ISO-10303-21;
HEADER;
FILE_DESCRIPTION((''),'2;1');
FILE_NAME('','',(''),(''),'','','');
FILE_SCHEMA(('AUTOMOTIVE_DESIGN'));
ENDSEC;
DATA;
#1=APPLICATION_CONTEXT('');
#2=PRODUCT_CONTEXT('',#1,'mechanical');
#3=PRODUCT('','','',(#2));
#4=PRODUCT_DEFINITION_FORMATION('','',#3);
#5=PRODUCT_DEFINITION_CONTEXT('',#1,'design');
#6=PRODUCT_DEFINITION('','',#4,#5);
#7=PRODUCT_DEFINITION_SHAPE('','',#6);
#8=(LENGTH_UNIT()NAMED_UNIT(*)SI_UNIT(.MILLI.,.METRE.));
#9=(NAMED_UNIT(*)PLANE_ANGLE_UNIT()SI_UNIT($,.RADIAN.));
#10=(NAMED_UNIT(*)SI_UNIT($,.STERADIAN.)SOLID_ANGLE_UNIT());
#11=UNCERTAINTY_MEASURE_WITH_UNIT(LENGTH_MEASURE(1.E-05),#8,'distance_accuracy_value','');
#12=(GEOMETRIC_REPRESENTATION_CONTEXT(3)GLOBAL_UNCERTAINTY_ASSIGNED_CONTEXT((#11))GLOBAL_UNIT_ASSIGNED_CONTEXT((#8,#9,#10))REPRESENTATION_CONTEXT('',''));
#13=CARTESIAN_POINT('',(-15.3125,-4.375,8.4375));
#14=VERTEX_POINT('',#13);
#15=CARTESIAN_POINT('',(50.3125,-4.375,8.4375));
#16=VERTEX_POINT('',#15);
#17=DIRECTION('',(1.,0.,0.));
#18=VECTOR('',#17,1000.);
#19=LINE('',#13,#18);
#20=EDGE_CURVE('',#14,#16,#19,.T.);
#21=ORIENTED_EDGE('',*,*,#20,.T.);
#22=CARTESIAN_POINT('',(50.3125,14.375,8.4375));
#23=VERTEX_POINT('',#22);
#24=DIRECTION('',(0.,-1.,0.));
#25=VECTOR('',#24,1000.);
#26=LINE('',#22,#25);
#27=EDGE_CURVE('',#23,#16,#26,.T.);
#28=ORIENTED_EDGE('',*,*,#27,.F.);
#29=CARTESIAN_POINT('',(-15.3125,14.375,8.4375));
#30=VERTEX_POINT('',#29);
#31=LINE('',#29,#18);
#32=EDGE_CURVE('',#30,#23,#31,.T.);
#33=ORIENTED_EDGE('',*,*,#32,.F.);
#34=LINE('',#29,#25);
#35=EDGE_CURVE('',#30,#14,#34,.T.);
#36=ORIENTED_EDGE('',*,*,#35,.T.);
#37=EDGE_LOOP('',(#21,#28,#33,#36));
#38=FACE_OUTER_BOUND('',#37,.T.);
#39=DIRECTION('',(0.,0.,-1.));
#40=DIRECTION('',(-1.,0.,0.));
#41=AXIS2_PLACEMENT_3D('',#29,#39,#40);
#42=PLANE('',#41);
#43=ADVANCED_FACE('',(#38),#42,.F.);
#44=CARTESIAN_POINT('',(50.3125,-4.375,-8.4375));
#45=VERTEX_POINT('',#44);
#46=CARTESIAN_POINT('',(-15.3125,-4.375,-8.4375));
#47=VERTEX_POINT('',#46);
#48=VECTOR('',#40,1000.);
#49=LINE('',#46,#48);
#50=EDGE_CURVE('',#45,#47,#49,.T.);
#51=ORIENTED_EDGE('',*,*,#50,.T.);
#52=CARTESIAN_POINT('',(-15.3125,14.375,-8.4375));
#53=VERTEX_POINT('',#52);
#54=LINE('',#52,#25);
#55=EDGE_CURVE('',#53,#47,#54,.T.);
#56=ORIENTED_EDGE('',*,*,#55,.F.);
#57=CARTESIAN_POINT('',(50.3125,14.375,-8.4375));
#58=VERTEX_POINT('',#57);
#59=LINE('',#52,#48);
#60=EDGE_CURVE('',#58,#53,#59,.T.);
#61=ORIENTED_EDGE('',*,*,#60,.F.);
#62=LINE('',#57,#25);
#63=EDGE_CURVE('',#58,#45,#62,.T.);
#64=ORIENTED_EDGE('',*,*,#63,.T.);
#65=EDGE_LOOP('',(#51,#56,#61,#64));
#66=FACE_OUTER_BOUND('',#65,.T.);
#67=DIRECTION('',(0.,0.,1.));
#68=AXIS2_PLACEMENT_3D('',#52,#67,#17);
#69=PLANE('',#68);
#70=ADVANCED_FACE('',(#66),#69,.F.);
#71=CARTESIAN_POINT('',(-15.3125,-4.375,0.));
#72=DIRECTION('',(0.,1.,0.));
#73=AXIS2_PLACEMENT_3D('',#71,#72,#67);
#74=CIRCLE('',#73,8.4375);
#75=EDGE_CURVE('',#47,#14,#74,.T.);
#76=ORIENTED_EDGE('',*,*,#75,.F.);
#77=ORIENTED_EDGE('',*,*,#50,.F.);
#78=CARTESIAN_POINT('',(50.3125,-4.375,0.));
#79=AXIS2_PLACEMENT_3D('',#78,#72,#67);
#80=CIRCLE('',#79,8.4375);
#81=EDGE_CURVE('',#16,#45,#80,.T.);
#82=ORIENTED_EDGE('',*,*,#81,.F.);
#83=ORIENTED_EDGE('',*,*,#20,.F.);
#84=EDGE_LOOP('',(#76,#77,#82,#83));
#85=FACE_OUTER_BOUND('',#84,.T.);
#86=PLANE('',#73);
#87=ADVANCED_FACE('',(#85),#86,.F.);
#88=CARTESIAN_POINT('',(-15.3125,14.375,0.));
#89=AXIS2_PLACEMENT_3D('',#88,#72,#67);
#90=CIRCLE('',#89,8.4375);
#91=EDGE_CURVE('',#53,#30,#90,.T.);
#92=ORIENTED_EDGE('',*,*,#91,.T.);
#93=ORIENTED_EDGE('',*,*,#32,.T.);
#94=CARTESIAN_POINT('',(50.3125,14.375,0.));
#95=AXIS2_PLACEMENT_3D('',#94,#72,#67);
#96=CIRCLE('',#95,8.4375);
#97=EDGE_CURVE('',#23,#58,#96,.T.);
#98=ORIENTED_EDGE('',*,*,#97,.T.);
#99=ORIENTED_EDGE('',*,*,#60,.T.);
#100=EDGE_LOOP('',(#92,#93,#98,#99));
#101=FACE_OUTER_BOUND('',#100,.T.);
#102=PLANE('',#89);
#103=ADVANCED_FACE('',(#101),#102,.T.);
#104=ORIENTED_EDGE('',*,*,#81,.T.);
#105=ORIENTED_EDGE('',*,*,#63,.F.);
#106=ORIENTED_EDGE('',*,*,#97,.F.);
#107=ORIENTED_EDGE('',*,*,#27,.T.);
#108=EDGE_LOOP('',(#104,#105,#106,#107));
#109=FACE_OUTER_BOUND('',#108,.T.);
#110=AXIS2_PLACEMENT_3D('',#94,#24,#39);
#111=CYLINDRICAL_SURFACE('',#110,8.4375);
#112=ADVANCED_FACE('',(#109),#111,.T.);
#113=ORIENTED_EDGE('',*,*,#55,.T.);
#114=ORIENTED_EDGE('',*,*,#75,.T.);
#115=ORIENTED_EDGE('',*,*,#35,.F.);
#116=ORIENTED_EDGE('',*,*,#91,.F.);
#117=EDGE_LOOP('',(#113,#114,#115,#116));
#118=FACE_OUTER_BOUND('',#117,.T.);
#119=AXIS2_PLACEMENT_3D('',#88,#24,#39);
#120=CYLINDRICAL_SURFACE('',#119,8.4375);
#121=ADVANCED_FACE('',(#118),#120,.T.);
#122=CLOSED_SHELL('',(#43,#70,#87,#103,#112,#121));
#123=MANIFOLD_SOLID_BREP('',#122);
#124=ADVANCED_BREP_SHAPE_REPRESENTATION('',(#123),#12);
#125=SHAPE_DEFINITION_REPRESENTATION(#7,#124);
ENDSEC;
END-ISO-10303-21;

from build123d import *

# Parameters (mm, degrees)
BOSS_EXTRUDE1_DEPTH = 10
SCALE_1_SCALE       = 1.875


with BuildPart() as part:
    # Sketch1 → Boss-Extrude1 (new body)
    with BuildSketch(Plane(origin=(0, 0, 0), x_dir=(1, 0, 0), z_dir=(0, 1, 0))):
        with BuildLine():
            Line((0, 4.5), (35, 4.5))
            ThreePointArc((35, 4.5), (39.5, 0), (35, -4.5))
            Line((35, -4.5), (0, -4.5))
            ThreePointArc((0, -4.5), (-4.5, 0), (0, 4.5))
        make_face()
    extrude(amount=BOSS_EXTRUDE1_DEPTH)


with BuildPart() as part_1:
    # Scale 1: scaled about (17.5, 5, 0)
    add(part.part.scale(SCALE_1_SCALE).moved(Location((-15.3125, -4.375, 0))))


solid = part_1.part
